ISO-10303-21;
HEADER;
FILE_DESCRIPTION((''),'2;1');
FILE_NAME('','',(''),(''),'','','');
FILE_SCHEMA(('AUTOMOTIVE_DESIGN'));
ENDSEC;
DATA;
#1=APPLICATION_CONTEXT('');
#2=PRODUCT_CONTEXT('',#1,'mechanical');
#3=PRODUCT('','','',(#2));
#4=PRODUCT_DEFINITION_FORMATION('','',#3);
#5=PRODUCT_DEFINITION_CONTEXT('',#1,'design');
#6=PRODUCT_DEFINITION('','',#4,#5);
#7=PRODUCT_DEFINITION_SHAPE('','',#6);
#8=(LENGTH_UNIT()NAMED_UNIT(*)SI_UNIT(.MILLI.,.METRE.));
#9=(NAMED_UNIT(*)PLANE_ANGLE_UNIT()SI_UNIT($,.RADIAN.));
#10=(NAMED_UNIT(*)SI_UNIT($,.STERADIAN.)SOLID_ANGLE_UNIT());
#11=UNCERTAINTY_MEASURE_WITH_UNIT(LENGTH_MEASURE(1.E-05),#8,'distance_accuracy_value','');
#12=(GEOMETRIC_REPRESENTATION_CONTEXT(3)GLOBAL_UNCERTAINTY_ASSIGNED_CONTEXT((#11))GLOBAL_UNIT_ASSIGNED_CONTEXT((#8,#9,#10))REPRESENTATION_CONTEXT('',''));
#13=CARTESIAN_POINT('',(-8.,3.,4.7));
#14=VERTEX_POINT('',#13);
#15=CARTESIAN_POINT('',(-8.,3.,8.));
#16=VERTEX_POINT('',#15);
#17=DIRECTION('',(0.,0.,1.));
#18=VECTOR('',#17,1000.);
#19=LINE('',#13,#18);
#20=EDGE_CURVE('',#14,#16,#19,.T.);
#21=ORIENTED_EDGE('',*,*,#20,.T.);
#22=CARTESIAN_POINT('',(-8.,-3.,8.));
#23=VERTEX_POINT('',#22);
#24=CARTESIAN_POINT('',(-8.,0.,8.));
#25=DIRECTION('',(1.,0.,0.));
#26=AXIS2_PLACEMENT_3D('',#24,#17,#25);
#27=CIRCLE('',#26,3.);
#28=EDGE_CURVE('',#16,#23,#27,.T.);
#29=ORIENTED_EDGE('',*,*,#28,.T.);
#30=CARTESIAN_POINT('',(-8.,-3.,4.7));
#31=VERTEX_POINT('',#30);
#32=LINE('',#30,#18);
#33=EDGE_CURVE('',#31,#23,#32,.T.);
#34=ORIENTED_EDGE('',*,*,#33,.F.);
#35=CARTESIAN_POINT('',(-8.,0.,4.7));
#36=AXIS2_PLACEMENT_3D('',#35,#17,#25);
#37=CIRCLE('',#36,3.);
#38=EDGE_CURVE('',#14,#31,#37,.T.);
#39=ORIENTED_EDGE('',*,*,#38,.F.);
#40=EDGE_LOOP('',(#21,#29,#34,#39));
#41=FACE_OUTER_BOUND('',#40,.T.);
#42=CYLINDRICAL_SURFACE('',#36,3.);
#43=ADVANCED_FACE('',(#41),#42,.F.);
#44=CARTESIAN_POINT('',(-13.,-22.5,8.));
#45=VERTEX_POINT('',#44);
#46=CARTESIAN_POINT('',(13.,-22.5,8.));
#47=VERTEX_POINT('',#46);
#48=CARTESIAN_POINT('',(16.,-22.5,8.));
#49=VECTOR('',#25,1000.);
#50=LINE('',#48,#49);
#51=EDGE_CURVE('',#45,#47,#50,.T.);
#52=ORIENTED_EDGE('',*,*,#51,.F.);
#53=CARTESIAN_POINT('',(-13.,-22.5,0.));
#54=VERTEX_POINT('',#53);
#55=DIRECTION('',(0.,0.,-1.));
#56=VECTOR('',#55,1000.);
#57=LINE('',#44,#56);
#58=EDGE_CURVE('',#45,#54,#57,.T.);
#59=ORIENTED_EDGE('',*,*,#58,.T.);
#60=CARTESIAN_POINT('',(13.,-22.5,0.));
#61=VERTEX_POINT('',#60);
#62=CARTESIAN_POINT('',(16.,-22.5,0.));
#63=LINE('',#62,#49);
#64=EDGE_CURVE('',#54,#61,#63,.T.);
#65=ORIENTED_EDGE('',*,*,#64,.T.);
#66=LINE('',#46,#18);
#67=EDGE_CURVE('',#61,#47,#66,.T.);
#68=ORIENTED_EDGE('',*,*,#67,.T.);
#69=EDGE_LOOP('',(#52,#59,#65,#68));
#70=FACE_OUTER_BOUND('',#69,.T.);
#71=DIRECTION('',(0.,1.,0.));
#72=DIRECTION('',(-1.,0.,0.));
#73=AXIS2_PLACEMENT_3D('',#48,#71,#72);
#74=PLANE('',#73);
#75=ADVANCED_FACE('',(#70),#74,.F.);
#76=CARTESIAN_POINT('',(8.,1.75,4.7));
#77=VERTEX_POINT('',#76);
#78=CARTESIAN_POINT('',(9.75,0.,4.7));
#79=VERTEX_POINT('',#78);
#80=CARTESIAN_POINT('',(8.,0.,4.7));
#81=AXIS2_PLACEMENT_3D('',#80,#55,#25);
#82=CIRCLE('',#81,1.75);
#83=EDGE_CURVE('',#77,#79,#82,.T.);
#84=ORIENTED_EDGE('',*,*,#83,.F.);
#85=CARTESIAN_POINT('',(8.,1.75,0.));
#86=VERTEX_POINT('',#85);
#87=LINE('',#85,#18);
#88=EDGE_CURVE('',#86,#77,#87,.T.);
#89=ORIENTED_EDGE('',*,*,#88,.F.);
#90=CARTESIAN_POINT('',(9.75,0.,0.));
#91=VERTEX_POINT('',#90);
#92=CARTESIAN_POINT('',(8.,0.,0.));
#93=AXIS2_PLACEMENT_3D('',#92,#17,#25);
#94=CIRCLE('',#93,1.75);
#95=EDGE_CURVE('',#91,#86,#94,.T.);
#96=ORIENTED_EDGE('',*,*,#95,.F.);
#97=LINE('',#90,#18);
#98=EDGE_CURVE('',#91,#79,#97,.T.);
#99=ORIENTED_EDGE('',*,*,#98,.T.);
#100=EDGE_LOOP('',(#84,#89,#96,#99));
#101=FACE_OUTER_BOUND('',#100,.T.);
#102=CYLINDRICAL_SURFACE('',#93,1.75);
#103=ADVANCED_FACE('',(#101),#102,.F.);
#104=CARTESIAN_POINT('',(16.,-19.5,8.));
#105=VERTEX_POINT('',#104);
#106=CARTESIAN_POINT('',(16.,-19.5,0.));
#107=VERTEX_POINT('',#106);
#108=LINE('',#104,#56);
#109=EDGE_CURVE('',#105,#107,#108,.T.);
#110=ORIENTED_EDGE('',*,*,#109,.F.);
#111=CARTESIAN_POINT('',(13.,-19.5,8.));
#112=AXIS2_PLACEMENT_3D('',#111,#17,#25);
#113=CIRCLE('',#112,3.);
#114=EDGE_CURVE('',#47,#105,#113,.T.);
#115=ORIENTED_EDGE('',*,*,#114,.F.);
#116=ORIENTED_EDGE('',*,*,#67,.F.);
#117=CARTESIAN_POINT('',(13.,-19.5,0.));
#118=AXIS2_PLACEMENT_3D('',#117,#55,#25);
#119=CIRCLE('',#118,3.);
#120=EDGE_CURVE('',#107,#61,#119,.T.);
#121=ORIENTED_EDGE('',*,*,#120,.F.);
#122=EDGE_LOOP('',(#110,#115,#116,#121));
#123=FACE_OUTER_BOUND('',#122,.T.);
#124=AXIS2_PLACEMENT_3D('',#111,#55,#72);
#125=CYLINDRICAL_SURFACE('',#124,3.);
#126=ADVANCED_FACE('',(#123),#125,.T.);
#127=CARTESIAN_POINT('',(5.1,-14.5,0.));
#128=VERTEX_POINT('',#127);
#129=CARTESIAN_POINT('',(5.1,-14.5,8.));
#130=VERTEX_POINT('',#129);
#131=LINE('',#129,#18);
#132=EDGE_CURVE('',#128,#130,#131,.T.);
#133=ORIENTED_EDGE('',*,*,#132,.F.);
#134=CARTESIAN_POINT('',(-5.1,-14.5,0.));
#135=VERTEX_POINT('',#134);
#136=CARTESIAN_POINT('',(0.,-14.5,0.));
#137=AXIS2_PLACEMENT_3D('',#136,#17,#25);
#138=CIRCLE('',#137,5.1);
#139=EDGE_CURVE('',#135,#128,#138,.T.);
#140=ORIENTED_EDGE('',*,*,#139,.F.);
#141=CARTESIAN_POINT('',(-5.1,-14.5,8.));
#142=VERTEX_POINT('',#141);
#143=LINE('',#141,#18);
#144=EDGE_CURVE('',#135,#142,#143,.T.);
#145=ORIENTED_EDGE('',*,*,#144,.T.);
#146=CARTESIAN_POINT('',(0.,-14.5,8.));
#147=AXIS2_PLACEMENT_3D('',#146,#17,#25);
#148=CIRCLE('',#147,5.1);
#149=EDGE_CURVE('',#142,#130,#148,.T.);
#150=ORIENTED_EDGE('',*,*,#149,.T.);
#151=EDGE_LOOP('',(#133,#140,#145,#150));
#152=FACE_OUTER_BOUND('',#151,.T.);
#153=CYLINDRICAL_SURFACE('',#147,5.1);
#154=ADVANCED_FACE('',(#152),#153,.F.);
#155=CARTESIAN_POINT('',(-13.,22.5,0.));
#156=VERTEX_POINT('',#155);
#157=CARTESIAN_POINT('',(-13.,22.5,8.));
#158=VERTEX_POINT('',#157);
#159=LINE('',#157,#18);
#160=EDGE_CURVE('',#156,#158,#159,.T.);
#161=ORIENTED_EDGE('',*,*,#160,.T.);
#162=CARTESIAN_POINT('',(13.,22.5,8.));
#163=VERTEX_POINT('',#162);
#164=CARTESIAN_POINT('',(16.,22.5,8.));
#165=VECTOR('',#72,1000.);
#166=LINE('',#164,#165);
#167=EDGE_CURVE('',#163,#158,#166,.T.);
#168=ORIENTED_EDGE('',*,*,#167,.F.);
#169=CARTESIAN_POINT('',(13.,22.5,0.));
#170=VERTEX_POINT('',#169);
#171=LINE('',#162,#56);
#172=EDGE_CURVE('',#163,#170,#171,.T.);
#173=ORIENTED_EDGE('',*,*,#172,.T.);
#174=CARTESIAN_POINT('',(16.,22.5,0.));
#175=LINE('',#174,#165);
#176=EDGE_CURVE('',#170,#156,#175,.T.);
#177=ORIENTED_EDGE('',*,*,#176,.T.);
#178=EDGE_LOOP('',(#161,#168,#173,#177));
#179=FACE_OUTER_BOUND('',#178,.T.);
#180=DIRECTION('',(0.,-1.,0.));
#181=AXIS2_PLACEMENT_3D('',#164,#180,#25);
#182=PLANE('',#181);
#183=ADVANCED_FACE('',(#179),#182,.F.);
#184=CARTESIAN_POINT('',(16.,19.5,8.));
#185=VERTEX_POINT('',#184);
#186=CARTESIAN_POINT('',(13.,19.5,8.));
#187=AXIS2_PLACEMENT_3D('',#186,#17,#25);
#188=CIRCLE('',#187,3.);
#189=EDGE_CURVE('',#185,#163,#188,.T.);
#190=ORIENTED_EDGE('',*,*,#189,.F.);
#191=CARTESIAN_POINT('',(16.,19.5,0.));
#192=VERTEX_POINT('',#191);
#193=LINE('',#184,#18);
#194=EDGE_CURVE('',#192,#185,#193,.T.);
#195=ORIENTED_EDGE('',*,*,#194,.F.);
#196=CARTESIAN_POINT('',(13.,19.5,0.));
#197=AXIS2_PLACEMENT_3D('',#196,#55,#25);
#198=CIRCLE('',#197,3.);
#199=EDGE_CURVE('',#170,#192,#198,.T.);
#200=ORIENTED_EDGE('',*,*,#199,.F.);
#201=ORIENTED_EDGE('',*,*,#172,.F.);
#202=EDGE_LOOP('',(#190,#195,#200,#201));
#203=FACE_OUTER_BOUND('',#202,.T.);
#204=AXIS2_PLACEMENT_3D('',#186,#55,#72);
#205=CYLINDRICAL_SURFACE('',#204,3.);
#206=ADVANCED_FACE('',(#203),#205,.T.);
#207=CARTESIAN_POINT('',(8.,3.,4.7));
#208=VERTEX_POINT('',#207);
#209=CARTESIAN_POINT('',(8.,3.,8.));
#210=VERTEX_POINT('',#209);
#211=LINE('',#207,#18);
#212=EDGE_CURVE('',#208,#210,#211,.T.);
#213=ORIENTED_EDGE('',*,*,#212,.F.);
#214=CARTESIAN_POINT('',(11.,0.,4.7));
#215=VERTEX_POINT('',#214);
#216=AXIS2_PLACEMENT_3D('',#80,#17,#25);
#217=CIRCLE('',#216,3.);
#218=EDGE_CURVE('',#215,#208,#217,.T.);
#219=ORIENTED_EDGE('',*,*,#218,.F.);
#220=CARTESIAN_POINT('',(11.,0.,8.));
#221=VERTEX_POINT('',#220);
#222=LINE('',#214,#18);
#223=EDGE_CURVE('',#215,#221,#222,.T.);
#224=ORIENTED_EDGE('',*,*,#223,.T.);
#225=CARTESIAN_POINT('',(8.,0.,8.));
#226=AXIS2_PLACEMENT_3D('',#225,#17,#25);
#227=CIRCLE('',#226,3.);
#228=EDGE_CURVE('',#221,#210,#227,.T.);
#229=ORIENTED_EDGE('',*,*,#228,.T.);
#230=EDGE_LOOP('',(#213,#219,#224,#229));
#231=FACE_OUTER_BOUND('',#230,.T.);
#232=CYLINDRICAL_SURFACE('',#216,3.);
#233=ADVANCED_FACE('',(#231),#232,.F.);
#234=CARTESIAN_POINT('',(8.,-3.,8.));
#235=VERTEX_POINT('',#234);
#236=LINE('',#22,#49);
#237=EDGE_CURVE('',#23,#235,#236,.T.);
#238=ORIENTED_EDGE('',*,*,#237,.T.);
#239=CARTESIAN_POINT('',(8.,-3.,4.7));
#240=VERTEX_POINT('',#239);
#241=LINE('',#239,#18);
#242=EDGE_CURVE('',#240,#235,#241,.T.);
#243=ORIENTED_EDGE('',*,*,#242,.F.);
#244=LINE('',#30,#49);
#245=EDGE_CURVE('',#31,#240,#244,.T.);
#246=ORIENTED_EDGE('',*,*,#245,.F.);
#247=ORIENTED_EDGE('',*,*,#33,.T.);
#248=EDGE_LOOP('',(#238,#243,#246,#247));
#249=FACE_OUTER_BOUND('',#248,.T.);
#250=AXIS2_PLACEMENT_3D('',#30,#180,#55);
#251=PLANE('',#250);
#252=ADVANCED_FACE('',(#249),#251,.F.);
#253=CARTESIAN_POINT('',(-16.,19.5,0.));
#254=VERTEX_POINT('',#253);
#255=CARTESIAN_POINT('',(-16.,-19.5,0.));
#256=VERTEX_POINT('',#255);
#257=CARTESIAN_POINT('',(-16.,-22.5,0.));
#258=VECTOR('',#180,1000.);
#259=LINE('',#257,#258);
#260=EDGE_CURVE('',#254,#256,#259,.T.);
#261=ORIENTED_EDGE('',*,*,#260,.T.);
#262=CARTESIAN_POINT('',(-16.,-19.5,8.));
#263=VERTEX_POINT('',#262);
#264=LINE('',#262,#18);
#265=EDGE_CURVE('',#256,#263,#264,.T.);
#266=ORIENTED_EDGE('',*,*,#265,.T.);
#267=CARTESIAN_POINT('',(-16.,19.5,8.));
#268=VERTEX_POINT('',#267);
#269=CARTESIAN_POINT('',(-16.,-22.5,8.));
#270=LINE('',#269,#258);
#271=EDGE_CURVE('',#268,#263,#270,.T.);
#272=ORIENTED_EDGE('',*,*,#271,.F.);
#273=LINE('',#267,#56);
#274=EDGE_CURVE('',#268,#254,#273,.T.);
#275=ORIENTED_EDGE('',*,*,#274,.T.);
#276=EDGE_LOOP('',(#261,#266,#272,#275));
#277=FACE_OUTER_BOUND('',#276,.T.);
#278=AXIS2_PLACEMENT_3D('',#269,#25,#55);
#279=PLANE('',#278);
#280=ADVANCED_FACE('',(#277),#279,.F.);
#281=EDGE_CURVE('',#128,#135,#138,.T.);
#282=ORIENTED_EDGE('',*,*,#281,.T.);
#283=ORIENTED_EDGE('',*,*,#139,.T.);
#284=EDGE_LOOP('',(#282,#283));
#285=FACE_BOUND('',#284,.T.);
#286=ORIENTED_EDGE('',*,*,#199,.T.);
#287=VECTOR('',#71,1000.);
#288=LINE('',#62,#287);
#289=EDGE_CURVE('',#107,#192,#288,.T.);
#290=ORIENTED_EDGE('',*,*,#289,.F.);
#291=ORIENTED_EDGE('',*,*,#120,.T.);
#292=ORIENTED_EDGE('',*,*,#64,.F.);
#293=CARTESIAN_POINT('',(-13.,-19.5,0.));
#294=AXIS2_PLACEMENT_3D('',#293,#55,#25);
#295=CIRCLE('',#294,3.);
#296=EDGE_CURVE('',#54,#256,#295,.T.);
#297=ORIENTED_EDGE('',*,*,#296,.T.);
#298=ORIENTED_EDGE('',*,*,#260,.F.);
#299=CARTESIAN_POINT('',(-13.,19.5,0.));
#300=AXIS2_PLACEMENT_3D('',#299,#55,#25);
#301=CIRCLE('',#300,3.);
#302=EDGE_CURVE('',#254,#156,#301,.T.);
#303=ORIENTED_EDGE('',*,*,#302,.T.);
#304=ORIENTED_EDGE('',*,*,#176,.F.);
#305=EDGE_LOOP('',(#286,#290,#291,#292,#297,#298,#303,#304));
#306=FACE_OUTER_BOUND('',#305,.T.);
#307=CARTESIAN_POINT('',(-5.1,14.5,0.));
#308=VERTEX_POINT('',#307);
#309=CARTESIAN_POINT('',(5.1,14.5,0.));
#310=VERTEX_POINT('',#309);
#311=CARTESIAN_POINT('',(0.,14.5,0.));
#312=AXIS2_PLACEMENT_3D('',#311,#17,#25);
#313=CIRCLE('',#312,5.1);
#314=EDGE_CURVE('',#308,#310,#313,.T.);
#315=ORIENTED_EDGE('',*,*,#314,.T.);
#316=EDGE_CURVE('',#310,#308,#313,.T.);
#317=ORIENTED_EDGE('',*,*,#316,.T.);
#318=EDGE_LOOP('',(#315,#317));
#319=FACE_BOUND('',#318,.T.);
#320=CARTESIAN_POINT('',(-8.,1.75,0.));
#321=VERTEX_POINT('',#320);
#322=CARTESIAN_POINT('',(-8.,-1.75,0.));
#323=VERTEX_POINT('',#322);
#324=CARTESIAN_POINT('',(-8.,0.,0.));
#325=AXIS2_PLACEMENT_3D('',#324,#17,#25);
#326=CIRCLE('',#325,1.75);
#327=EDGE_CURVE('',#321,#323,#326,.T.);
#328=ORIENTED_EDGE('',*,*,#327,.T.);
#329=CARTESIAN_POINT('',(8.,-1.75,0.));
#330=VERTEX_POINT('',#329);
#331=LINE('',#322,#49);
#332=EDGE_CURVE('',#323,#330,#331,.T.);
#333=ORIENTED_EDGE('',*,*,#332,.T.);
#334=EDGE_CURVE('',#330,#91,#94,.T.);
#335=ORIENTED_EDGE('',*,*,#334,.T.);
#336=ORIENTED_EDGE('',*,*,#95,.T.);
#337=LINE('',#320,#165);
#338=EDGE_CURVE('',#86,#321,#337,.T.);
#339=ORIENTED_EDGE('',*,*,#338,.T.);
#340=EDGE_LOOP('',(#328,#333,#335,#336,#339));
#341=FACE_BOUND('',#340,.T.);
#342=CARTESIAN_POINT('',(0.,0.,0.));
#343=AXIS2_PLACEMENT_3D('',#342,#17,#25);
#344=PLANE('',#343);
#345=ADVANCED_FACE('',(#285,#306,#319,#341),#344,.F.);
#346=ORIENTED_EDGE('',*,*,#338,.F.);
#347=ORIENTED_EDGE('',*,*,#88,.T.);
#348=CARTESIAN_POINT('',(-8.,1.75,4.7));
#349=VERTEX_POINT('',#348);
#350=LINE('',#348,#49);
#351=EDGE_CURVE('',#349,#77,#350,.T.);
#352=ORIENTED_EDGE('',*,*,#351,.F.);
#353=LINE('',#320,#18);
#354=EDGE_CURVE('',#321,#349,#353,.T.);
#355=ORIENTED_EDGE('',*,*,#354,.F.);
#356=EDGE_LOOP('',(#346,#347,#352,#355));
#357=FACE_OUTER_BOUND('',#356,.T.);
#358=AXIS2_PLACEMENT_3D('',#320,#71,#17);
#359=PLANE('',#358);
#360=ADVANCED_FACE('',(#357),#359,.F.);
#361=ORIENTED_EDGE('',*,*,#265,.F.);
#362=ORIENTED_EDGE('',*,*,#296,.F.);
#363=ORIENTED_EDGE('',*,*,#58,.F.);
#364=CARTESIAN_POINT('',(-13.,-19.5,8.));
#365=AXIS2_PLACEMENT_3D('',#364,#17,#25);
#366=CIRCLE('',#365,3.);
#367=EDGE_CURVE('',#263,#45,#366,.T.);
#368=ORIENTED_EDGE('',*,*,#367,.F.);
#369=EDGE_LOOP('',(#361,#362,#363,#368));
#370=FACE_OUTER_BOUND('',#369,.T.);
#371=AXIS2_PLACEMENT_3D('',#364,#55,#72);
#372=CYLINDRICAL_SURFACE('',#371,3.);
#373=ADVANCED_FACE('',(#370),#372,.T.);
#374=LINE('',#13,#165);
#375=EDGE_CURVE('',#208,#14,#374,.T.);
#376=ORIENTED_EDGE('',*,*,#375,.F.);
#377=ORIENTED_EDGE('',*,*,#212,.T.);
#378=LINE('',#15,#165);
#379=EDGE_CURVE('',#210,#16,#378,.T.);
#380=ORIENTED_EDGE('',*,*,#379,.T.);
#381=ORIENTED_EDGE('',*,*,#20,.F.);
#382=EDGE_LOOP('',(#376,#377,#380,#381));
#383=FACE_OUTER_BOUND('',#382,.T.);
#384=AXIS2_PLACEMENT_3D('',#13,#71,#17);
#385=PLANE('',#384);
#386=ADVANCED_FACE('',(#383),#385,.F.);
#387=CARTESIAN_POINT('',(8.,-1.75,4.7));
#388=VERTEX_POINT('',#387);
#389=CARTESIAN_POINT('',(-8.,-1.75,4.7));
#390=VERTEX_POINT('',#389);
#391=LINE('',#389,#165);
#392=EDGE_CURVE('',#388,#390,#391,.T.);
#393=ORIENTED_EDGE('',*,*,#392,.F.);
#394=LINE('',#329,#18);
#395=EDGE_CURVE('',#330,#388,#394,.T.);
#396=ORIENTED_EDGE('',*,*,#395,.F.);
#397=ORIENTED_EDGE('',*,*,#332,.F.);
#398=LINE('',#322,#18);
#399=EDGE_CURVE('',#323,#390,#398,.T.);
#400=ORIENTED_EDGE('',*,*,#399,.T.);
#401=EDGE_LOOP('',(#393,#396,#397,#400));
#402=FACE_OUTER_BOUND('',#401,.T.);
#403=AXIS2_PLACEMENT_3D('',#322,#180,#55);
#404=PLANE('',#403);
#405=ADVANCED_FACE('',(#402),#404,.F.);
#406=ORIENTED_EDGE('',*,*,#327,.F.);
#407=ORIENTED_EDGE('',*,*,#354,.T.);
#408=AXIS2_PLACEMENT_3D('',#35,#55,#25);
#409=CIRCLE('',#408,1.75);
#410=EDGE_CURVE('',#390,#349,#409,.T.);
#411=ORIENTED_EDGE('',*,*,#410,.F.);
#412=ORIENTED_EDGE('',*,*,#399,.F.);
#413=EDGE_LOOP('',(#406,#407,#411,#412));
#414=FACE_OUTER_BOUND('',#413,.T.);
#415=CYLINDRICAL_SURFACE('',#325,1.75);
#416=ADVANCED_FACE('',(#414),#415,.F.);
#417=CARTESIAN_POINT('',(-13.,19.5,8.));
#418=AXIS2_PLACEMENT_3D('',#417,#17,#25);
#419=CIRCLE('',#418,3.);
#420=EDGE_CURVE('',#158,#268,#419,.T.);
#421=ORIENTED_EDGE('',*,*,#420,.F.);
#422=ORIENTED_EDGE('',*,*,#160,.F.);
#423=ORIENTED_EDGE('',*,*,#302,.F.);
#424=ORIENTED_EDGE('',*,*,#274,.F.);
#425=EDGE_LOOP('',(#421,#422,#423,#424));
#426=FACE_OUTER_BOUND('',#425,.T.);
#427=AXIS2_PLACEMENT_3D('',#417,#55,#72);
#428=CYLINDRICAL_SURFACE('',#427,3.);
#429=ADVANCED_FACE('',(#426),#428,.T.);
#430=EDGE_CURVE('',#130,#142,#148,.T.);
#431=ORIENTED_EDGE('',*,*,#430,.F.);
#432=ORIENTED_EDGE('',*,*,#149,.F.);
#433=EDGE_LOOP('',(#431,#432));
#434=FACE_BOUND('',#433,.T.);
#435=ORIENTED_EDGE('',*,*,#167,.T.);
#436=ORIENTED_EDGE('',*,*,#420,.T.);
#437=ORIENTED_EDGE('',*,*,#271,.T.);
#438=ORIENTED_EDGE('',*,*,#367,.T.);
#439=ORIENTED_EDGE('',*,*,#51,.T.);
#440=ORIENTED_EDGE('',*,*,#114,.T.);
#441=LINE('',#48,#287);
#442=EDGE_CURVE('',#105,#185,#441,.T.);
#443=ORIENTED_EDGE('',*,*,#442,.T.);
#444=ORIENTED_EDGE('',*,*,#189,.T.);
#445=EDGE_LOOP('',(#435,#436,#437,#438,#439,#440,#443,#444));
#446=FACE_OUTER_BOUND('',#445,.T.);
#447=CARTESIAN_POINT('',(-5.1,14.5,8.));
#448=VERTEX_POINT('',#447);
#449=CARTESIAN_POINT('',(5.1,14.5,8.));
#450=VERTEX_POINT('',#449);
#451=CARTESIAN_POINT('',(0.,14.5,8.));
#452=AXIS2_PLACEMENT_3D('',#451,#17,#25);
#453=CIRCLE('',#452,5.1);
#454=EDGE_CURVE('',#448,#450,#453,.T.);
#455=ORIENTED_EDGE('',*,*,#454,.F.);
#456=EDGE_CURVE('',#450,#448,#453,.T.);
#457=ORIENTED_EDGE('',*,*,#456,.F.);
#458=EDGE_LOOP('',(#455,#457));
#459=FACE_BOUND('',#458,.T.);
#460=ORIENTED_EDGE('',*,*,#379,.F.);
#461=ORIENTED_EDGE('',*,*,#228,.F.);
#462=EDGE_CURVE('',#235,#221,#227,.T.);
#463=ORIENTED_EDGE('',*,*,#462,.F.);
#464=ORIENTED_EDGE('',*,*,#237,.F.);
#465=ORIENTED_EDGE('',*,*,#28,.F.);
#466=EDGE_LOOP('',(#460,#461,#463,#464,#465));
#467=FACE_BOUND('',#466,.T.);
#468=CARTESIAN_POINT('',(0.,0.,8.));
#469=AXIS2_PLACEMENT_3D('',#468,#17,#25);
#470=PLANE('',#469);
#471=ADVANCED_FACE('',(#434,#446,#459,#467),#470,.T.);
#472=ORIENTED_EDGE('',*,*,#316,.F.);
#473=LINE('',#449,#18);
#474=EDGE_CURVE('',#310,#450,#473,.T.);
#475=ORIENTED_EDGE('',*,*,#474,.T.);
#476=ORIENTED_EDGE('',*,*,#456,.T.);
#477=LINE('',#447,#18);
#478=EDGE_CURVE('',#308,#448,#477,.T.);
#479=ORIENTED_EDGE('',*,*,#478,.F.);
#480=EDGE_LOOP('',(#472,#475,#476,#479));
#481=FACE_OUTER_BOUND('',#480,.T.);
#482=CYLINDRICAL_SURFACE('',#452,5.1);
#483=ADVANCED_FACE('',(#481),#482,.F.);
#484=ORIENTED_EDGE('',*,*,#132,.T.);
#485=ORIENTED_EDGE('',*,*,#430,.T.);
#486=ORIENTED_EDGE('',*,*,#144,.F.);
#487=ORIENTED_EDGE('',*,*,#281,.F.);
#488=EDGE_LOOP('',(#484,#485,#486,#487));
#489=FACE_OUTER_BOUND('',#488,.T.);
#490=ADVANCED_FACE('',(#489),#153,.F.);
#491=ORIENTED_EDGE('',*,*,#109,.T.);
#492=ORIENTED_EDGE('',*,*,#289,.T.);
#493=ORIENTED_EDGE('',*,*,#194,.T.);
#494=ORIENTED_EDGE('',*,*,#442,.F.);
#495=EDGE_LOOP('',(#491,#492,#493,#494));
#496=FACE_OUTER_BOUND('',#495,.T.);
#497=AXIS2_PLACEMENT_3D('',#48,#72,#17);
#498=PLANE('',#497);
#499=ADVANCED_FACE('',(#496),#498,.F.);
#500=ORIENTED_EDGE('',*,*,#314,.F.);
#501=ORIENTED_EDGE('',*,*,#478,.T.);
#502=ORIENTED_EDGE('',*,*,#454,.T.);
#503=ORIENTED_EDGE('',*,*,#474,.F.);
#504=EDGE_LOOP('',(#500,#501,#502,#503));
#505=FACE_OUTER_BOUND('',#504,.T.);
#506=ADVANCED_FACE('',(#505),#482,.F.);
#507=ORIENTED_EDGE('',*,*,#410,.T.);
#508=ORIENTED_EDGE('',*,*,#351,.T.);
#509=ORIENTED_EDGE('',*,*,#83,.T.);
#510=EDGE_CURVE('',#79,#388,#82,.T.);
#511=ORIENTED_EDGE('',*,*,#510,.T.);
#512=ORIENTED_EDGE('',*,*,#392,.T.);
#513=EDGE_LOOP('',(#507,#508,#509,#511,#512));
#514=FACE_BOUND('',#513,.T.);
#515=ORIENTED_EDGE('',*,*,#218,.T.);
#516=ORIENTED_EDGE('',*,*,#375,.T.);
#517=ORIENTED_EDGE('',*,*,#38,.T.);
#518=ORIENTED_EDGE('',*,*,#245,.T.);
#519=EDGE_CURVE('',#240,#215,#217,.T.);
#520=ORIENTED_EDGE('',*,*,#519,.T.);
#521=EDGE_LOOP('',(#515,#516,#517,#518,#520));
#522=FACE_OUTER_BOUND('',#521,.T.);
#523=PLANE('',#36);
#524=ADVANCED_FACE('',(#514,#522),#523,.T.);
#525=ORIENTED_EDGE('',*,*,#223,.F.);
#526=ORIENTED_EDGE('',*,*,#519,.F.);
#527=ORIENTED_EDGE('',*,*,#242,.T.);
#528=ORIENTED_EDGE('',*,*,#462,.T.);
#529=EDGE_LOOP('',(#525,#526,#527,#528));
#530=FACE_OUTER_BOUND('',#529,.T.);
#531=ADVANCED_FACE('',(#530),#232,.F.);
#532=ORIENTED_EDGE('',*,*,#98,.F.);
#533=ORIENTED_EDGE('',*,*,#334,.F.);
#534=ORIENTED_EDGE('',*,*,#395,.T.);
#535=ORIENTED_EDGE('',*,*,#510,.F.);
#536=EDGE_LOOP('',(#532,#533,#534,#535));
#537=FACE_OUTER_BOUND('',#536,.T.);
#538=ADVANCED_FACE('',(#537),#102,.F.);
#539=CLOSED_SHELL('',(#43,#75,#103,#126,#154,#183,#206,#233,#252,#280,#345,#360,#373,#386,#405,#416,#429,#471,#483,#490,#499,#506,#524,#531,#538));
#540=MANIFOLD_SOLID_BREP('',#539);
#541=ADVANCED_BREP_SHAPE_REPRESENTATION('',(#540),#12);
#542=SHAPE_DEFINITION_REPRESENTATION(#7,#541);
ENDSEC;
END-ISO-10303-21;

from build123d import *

# Parameters (mm, degrees)
SKETCH1_W           = 32
SKETCH1_H           = 45
BOSS_EXTRUDE1_DEPTH = 8
CUT_EXTRUDE1_DEPTH  = 29.744564704
CUT_EXTRUDE2_DEPTH  = 3.3
FILLET1_R           = 3
M12_TAPPED_HOLE2_D  = 10.2


with BuildPart() as part:
    # Sketch1 → Boss-Extrude1 (new body)
    with BuildSketch(Plane.XY):
        Rectangle(SKETCH1_W, SKETCH1_H)
    extrude(amount=BOSS_EXTRUDE1_DEPTH)

    # Sketch5 → Cut-Extrude1 (cut, through all)
    with BuildSketch(Plane.XY.offset(8)):
        with BuildLine():
            Line((-8, 1.75), (8, 1.75))
            ThreePointArc((8, 1.75), (9.75, 0), (8, -1.75))
            Line((8, -1.75), (-8, -1.75))
            ThreePointArc((-8, -1.75), (-9.75, 0), (-8, 1.75))
        make_face()
    extrude(amount=-CUT_EXTRUDE1_DEPTH, mode=Mode.SUBTRACT)

    # Sketch6 → Cut-Extrude2 (cut)
    with BuildSketch(Plane.XY.offset(8)):
        with BuildLine():
            Line((-8, 3), (8, 3))
            ThreePointArc((8, 3), (11, 0), (8, -3))
            Line((8, -3), (-8, -3))
            ThreePointArc((-8, -3), (-11, 0), (-8, 3))
        make_face()
    extrude(amount=-CUT_EXTRUDE2_DEPTH, mode=Mode.SUBTRACT)

    # Fillet1
    fillet1_edges = [part.edges().sort_by_distance(p)[0] for p in [
        (-16, 22.5, 4),
        (16, 22.5, 4),
        (16, -22.5, 4),
        (-16, -22.5, 4),
    ]]
    fillet(fillet1_edges, radius=FILLET1_R)

    # M12 Tapped Hole2 (through all)
    with Locations(Plane.XY.offset(8)):
        with Locations((0, -14.5), (0, 14.5)):
            Hole(M12_TAPPED_HOLE2_D / 2)


solid = part.part
